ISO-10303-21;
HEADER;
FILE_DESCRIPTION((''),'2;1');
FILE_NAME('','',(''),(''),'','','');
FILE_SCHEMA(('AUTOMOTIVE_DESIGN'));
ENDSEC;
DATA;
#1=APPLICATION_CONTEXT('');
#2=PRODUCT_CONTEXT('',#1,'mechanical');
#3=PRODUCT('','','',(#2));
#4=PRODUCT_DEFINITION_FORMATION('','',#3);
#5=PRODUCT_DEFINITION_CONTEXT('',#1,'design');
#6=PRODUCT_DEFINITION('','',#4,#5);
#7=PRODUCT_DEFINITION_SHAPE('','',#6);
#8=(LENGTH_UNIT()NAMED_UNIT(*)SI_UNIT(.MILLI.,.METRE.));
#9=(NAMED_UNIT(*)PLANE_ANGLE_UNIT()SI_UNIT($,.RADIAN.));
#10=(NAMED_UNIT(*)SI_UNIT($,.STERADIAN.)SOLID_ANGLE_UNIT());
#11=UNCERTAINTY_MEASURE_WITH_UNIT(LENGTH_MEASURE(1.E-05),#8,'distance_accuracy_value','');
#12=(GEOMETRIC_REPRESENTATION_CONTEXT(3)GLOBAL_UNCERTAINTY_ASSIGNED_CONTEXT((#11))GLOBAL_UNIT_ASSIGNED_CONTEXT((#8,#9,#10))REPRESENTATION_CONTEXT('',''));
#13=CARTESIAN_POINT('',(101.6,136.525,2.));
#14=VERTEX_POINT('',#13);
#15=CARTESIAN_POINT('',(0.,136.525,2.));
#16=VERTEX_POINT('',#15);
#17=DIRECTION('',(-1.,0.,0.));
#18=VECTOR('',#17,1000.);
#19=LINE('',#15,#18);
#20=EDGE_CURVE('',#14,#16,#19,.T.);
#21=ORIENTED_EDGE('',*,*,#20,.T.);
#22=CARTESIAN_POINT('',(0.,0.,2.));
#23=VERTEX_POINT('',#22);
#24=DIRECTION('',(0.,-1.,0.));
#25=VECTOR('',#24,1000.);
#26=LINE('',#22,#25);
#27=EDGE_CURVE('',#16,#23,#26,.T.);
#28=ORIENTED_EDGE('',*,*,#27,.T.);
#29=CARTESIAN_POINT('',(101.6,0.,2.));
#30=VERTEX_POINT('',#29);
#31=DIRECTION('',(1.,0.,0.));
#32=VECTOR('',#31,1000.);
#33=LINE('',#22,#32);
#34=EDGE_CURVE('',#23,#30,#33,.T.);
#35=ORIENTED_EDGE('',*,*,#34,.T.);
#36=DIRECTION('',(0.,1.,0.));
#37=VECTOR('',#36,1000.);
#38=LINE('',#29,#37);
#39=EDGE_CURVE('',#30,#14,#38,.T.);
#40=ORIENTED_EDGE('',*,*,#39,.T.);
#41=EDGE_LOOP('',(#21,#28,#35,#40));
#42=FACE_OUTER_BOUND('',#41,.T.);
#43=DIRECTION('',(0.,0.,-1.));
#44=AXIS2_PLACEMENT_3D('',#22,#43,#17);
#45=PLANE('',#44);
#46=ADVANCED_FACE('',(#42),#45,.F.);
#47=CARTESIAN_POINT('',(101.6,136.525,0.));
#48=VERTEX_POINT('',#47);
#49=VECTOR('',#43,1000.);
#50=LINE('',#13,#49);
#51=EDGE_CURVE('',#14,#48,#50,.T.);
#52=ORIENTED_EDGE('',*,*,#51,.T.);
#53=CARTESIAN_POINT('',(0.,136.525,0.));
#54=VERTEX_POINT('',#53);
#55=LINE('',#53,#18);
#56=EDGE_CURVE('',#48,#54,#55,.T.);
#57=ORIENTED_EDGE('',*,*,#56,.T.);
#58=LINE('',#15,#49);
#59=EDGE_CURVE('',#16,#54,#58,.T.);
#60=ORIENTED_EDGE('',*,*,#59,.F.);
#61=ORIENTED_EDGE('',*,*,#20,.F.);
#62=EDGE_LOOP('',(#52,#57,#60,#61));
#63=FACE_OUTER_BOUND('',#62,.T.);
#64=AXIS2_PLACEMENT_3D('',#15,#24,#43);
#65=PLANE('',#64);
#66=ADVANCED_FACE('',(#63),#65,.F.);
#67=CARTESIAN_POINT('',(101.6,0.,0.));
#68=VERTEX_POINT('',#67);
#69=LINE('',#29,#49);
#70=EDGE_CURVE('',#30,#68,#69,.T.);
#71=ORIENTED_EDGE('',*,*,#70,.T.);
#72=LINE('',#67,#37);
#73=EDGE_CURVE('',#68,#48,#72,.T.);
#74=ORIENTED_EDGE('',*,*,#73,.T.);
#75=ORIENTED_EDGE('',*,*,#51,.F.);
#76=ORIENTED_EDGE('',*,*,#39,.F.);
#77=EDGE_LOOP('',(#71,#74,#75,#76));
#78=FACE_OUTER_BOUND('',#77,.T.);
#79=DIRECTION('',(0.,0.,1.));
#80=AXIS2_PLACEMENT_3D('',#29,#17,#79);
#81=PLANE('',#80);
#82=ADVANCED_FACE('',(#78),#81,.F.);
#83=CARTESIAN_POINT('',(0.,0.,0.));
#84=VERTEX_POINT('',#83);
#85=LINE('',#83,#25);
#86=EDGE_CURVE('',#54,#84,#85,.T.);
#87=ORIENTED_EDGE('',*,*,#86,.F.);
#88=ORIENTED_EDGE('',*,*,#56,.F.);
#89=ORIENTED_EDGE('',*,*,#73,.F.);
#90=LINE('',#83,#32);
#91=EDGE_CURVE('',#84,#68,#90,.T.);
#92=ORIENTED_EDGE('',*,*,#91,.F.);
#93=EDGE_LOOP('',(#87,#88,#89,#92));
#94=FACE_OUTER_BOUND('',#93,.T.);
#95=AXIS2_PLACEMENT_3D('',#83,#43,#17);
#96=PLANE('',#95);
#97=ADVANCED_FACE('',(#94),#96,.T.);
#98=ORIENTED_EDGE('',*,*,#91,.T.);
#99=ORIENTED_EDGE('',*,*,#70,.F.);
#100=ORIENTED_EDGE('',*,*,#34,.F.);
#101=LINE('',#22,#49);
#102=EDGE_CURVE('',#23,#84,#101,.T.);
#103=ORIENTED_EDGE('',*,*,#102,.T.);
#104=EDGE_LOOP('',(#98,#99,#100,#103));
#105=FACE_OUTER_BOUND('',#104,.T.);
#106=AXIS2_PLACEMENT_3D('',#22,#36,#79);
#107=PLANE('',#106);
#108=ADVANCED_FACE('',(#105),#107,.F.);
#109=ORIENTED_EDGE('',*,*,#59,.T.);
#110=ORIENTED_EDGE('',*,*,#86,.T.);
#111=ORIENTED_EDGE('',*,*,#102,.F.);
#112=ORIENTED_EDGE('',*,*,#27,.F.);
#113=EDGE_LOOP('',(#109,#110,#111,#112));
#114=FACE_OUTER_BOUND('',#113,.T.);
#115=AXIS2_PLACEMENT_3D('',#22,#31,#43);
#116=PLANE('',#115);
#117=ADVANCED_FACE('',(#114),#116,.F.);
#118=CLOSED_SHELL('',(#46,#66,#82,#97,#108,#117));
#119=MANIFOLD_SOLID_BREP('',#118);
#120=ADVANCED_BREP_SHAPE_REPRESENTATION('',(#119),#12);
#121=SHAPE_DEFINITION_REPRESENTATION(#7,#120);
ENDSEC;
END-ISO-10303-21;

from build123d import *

# Parameters (mm, degrees)
SKETCH1_W      = 101.6
SKETCH1_H      = 136.525
EXTRUDE1_DEPTH = 2


with BuildPart() as part:
    # Sketch1 → Extrude1 (new body)
    with BuildSketch(Plane.XY):
        with Locations((50.8, 68.2625)):
            Rectangle(SKETCH1_W, SKETCH1_H)
    extrude(amount=EXTRUDE1_DEPTH)


solid = part.part
